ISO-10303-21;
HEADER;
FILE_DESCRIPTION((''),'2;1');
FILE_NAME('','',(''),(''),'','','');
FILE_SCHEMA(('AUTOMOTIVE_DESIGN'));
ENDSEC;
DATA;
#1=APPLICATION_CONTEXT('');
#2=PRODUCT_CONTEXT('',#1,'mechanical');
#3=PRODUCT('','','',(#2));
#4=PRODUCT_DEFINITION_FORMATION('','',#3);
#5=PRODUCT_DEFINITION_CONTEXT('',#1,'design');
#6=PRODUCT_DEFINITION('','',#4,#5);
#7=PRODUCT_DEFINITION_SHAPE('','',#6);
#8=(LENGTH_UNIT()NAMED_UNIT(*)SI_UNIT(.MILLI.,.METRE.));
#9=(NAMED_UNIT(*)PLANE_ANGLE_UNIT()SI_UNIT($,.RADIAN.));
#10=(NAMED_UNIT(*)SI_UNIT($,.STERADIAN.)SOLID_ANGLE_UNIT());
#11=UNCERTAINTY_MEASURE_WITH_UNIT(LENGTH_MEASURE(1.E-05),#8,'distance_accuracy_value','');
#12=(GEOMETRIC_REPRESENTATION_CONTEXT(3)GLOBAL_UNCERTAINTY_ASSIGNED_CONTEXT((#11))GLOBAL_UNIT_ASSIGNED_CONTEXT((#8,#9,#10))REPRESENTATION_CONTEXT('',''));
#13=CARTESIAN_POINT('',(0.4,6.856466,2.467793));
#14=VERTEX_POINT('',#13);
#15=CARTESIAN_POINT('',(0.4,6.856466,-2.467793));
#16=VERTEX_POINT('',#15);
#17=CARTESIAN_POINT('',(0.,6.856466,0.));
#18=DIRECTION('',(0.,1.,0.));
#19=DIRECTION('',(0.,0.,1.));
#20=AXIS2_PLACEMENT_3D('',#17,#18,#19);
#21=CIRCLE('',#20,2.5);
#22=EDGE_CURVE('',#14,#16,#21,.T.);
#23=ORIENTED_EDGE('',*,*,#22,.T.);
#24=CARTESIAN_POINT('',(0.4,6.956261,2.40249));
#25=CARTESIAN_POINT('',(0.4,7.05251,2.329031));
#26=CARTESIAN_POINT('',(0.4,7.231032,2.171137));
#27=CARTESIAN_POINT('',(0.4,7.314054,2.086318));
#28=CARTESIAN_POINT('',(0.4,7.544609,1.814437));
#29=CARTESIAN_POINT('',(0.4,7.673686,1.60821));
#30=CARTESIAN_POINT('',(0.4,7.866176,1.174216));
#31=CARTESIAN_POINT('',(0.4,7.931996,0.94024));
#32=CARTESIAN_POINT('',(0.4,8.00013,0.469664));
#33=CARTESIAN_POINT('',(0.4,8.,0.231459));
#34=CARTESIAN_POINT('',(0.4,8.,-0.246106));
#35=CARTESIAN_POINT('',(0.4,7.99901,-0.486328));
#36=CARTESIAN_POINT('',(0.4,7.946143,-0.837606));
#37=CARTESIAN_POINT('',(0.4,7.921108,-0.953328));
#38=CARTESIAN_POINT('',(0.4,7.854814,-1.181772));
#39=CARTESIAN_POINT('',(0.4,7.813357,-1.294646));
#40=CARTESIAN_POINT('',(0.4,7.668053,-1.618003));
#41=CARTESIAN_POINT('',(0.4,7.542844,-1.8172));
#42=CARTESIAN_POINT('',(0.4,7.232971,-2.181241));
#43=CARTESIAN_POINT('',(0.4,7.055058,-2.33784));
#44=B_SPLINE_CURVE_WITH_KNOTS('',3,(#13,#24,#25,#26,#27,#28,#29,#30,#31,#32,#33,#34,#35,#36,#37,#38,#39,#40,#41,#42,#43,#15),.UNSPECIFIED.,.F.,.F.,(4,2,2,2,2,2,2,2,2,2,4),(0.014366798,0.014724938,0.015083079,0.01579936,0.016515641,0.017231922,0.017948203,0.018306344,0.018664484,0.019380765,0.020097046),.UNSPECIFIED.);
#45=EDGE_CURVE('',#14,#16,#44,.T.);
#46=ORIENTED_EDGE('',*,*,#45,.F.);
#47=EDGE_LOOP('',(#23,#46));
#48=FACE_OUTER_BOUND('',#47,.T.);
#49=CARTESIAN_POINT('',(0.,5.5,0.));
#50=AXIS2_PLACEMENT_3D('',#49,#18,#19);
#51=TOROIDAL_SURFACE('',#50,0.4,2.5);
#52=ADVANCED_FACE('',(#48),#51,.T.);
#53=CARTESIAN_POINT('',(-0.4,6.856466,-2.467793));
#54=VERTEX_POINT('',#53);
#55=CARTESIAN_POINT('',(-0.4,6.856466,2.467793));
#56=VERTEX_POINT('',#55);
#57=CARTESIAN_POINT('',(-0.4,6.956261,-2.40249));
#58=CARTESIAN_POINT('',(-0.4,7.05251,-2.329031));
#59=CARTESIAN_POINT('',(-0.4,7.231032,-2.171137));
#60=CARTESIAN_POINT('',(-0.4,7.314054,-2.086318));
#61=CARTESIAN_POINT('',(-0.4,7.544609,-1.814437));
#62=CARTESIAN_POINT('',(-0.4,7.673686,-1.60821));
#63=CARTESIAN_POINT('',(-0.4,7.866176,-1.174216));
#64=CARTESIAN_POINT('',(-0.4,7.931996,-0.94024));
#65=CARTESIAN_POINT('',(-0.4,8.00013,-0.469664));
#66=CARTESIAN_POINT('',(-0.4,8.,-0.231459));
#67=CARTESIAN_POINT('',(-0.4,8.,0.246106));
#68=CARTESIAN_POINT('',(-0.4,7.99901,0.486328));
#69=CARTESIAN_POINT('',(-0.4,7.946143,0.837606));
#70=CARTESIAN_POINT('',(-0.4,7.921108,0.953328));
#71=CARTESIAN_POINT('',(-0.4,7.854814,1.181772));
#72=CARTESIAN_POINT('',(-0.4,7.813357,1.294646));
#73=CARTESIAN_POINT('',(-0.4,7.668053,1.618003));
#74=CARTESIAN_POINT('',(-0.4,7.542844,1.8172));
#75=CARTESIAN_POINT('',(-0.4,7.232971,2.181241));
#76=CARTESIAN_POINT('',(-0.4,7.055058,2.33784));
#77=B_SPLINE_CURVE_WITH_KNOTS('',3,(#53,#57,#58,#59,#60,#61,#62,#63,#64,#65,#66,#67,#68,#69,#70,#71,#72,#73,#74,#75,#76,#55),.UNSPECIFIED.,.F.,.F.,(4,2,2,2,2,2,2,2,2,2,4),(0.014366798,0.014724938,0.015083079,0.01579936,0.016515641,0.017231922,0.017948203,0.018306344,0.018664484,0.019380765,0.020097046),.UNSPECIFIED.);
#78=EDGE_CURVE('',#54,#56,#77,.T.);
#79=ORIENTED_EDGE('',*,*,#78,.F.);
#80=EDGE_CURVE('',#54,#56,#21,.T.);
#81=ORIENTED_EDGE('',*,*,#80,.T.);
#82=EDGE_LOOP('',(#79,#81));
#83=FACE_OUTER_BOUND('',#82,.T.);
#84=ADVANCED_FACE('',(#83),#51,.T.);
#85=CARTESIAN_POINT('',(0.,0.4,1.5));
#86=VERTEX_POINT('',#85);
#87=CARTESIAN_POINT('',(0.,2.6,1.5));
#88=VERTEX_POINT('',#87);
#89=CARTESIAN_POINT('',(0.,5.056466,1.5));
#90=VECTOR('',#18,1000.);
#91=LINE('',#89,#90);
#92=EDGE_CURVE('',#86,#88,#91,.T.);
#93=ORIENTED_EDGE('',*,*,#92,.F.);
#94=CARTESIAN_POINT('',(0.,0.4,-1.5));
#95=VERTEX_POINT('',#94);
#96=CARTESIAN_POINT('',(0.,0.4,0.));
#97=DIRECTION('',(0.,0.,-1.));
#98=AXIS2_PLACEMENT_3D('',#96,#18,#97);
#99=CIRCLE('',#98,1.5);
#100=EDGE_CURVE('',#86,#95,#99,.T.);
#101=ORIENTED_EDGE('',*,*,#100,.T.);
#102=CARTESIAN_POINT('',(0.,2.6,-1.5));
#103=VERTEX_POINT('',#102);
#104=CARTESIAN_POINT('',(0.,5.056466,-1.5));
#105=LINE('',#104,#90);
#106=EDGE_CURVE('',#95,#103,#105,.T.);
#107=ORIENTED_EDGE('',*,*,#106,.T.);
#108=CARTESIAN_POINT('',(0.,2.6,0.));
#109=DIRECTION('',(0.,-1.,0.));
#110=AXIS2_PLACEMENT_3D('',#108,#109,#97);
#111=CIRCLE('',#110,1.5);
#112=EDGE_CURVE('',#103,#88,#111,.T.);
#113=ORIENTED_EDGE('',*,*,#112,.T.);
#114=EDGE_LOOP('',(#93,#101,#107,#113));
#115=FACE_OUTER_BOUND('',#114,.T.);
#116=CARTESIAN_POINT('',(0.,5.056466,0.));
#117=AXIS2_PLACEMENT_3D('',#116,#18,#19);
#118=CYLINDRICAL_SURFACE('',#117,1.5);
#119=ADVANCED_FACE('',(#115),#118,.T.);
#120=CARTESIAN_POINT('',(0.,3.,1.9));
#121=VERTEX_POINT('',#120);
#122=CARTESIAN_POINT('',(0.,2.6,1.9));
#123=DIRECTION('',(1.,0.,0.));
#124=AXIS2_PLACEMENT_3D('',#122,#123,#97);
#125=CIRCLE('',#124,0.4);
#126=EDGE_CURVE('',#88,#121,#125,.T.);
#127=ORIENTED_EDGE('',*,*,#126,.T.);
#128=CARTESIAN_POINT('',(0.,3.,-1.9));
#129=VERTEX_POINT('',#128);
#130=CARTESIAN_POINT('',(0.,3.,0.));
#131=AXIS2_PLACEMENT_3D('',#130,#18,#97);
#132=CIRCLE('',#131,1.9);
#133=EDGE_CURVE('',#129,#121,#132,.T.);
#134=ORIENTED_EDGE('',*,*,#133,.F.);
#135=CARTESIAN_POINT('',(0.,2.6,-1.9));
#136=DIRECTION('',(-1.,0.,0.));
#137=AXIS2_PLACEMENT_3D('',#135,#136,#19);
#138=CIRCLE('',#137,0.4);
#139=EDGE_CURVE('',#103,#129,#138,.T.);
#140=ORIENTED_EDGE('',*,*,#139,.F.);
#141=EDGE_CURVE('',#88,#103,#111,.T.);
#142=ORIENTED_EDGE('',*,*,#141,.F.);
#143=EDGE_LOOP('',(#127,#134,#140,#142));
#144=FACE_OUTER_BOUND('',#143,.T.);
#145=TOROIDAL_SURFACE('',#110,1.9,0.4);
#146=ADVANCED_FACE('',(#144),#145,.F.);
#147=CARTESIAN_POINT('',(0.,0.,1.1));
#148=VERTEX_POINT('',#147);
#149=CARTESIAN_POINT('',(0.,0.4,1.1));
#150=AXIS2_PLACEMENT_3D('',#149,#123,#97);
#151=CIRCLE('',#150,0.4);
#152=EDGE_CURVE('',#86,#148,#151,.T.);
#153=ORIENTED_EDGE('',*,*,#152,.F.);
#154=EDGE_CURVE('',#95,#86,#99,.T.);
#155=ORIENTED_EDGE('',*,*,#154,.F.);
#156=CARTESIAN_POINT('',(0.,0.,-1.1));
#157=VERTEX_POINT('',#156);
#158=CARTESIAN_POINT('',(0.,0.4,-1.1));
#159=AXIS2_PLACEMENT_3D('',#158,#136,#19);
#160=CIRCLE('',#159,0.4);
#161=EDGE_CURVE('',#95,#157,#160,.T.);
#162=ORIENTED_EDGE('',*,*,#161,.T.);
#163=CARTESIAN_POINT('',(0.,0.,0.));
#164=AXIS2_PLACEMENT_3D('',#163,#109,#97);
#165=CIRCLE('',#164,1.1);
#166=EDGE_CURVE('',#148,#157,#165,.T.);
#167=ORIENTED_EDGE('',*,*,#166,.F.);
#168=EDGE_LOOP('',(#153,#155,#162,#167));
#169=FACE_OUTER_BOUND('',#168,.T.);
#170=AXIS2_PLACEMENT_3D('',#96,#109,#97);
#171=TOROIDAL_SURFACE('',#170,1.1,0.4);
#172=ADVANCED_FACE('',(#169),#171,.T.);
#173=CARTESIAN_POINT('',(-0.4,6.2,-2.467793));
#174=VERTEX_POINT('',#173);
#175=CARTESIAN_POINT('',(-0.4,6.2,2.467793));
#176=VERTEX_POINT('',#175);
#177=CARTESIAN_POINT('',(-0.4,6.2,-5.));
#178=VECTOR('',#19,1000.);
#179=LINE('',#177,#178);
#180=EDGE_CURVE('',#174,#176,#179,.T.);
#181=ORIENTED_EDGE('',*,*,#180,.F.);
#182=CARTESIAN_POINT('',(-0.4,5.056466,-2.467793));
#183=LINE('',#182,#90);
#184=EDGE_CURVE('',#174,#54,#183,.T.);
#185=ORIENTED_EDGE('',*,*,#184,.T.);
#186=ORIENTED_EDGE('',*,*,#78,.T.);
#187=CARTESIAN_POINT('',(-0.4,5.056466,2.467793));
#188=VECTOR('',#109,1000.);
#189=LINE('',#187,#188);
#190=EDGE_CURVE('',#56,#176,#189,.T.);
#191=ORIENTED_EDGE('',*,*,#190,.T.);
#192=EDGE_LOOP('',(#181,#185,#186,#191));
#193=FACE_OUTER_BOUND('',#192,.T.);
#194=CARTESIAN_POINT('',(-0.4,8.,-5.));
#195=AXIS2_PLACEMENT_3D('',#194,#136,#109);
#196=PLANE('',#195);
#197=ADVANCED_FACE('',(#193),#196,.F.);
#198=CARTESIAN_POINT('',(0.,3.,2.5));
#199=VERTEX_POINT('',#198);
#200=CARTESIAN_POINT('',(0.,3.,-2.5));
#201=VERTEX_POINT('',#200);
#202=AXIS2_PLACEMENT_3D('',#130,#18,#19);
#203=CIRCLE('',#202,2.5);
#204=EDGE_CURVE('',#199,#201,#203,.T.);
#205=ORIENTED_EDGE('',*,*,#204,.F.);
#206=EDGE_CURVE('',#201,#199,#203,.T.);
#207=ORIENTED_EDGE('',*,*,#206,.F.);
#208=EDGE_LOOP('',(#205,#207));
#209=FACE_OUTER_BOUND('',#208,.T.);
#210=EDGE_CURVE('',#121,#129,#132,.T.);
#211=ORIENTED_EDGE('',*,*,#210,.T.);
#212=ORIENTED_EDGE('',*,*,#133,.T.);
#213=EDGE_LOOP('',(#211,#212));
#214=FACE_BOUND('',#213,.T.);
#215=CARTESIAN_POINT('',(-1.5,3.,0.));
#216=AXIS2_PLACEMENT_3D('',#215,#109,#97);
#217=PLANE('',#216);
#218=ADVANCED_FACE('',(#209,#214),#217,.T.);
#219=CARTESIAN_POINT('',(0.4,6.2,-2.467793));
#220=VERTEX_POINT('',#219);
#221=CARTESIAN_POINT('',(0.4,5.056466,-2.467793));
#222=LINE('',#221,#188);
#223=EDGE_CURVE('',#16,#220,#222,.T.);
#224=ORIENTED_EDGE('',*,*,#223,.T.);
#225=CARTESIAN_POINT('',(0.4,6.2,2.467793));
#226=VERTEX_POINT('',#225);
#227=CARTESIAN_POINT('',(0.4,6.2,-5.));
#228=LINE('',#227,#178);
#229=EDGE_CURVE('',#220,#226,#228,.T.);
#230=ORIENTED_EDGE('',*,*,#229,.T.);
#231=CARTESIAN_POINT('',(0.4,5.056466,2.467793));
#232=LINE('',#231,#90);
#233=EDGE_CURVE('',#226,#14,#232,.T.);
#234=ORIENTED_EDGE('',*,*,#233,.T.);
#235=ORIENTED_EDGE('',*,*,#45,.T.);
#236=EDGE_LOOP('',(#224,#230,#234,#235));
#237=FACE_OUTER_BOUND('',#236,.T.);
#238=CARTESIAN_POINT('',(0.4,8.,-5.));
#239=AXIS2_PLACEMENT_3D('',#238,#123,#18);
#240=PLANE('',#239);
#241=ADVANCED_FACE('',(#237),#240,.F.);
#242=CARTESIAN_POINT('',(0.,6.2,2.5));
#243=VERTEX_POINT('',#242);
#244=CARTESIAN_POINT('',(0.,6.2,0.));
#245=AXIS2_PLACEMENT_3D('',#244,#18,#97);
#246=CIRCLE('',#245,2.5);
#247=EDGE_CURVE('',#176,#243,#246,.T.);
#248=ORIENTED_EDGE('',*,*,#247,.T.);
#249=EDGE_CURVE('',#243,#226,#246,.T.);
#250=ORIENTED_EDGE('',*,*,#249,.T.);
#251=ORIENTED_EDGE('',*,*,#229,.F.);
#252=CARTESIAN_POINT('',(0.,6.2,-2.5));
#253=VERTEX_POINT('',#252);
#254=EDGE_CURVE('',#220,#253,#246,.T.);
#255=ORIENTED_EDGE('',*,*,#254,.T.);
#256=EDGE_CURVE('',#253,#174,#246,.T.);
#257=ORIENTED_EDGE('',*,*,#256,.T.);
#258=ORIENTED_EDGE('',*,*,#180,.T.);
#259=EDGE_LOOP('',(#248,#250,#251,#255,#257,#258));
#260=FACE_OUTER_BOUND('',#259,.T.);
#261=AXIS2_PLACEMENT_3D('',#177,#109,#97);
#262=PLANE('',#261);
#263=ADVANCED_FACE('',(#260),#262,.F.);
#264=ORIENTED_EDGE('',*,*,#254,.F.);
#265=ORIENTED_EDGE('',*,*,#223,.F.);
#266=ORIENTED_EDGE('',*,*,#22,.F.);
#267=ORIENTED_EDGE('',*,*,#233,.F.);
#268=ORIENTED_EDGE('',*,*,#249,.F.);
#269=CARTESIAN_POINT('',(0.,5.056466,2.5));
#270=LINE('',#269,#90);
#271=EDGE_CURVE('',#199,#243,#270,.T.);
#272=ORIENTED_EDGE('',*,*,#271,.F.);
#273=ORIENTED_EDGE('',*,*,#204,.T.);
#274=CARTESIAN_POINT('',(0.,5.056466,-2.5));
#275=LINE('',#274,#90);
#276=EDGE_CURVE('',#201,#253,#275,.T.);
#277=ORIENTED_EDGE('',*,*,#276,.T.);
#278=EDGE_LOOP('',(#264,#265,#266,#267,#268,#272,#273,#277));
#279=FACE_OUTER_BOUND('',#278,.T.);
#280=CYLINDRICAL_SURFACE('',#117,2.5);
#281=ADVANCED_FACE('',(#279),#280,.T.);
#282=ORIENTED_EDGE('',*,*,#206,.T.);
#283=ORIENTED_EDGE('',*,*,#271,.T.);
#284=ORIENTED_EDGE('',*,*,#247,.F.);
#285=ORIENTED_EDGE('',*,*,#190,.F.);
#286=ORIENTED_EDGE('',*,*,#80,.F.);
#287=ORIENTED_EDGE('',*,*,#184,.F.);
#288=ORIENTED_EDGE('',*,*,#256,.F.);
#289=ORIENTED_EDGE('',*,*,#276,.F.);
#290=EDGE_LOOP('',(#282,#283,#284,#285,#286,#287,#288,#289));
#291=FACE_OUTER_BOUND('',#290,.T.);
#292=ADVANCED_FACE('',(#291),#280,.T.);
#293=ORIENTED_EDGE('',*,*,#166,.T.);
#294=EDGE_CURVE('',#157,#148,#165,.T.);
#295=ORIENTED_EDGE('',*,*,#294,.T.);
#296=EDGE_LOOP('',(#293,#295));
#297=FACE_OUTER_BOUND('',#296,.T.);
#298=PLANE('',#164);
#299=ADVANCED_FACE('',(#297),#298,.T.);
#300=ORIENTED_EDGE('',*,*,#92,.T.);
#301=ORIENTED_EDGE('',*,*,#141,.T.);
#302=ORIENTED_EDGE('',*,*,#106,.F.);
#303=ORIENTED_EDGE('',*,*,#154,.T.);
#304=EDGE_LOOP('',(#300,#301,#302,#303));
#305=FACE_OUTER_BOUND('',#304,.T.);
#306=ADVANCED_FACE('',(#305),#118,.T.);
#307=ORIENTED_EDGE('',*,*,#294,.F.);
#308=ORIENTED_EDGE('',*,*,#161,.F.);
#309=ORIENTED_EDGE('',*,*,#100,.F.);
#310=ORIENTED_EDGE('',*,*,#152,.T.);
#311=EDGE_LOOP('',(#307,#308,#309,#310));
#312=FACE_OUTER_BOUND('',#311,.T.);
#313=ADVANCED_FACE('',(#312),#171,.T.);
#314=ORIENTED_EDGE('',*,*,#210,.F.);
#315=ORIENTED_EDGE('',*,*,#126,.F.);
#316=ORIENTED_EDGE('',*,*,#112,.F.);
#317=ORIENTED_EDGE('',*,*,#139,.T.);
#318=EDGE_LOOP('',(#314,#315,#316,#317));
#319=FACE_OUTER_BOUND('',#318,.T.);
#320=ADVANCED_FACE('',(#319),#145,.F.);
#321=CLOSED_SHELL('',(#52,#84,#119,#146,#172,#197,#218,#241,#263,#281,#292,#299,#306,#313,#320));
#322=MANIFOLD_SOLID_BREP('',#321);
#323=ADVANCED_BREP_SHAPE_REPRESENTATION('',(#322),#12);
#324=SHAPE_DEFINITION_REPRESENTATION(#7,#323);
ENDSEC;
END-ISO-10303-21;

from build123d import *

# Parameters (mm, degrees)
FILLET1_R          = 0.4
FILLET2_R          = 0.4
SKETCH3_W          = 0.8
SKETCH3_H          = 1.8
CUT_EXTRUDE1_DEPTH = 5


with BuildPart() as part:
    # Sketch1 → Revolve1 (revolve)
    with BuildSketch(Plane.XY, mode=Mode.PRIVATE) as revolve1_sk:
        with BuildLine():
            Line((0, 0), (-1.5, 0))
            Line((-1.5, 0), (-1.5, 3))
            Line((-1.5, 3), (-2.5, 3))
            Line((-2.5, 3), (-2.5, 6.856465997))
            ThreePointArc((-2.5, 6.856465997), (-1.595582496, 7.695582496), (-0.4, 8))
            Line((-0.4, 8), (0, 8))
            Line((0, 8), (0, 5.056465997))
            Line((0, 5.056465997), (0, 0))
        make_face()
    revolve(revolve1_sk.sketch.rotate(Axis((0, 5.056465997, 0), (0, -1, 0)), 270), axis=Axis((0, 5.056465997, 0), (0, -1, 0)))

    # Fillet1
    fillet1_edges = [part.edges().sort_by_distance(p)[0] for p in [
        (0, 3, -1.5),
    ]]
    fillet(fillet1_edges, radius=FILLET1_R)

    # Fillet2
    fillet2_edges = [part.edges().sort_by_distance(p)[0] for p in [
        (0, 0, -1.5),
    ]]
    fillet(fillet2_edges, radius=FILLET2_R)

    # Sketch3 → Cut-Extrude1 (cut, symmetric)
    with BuildSketch(Plane.XY):
        with Locations((0, 7.1)):
            Rectangle(SKETCH3_W, SKETCH3_H)
    extrude(amount=CUT_EXTRUDE1_DEPTH, both=True, mode=Mode.SUBTRACT)


solid = part.part
